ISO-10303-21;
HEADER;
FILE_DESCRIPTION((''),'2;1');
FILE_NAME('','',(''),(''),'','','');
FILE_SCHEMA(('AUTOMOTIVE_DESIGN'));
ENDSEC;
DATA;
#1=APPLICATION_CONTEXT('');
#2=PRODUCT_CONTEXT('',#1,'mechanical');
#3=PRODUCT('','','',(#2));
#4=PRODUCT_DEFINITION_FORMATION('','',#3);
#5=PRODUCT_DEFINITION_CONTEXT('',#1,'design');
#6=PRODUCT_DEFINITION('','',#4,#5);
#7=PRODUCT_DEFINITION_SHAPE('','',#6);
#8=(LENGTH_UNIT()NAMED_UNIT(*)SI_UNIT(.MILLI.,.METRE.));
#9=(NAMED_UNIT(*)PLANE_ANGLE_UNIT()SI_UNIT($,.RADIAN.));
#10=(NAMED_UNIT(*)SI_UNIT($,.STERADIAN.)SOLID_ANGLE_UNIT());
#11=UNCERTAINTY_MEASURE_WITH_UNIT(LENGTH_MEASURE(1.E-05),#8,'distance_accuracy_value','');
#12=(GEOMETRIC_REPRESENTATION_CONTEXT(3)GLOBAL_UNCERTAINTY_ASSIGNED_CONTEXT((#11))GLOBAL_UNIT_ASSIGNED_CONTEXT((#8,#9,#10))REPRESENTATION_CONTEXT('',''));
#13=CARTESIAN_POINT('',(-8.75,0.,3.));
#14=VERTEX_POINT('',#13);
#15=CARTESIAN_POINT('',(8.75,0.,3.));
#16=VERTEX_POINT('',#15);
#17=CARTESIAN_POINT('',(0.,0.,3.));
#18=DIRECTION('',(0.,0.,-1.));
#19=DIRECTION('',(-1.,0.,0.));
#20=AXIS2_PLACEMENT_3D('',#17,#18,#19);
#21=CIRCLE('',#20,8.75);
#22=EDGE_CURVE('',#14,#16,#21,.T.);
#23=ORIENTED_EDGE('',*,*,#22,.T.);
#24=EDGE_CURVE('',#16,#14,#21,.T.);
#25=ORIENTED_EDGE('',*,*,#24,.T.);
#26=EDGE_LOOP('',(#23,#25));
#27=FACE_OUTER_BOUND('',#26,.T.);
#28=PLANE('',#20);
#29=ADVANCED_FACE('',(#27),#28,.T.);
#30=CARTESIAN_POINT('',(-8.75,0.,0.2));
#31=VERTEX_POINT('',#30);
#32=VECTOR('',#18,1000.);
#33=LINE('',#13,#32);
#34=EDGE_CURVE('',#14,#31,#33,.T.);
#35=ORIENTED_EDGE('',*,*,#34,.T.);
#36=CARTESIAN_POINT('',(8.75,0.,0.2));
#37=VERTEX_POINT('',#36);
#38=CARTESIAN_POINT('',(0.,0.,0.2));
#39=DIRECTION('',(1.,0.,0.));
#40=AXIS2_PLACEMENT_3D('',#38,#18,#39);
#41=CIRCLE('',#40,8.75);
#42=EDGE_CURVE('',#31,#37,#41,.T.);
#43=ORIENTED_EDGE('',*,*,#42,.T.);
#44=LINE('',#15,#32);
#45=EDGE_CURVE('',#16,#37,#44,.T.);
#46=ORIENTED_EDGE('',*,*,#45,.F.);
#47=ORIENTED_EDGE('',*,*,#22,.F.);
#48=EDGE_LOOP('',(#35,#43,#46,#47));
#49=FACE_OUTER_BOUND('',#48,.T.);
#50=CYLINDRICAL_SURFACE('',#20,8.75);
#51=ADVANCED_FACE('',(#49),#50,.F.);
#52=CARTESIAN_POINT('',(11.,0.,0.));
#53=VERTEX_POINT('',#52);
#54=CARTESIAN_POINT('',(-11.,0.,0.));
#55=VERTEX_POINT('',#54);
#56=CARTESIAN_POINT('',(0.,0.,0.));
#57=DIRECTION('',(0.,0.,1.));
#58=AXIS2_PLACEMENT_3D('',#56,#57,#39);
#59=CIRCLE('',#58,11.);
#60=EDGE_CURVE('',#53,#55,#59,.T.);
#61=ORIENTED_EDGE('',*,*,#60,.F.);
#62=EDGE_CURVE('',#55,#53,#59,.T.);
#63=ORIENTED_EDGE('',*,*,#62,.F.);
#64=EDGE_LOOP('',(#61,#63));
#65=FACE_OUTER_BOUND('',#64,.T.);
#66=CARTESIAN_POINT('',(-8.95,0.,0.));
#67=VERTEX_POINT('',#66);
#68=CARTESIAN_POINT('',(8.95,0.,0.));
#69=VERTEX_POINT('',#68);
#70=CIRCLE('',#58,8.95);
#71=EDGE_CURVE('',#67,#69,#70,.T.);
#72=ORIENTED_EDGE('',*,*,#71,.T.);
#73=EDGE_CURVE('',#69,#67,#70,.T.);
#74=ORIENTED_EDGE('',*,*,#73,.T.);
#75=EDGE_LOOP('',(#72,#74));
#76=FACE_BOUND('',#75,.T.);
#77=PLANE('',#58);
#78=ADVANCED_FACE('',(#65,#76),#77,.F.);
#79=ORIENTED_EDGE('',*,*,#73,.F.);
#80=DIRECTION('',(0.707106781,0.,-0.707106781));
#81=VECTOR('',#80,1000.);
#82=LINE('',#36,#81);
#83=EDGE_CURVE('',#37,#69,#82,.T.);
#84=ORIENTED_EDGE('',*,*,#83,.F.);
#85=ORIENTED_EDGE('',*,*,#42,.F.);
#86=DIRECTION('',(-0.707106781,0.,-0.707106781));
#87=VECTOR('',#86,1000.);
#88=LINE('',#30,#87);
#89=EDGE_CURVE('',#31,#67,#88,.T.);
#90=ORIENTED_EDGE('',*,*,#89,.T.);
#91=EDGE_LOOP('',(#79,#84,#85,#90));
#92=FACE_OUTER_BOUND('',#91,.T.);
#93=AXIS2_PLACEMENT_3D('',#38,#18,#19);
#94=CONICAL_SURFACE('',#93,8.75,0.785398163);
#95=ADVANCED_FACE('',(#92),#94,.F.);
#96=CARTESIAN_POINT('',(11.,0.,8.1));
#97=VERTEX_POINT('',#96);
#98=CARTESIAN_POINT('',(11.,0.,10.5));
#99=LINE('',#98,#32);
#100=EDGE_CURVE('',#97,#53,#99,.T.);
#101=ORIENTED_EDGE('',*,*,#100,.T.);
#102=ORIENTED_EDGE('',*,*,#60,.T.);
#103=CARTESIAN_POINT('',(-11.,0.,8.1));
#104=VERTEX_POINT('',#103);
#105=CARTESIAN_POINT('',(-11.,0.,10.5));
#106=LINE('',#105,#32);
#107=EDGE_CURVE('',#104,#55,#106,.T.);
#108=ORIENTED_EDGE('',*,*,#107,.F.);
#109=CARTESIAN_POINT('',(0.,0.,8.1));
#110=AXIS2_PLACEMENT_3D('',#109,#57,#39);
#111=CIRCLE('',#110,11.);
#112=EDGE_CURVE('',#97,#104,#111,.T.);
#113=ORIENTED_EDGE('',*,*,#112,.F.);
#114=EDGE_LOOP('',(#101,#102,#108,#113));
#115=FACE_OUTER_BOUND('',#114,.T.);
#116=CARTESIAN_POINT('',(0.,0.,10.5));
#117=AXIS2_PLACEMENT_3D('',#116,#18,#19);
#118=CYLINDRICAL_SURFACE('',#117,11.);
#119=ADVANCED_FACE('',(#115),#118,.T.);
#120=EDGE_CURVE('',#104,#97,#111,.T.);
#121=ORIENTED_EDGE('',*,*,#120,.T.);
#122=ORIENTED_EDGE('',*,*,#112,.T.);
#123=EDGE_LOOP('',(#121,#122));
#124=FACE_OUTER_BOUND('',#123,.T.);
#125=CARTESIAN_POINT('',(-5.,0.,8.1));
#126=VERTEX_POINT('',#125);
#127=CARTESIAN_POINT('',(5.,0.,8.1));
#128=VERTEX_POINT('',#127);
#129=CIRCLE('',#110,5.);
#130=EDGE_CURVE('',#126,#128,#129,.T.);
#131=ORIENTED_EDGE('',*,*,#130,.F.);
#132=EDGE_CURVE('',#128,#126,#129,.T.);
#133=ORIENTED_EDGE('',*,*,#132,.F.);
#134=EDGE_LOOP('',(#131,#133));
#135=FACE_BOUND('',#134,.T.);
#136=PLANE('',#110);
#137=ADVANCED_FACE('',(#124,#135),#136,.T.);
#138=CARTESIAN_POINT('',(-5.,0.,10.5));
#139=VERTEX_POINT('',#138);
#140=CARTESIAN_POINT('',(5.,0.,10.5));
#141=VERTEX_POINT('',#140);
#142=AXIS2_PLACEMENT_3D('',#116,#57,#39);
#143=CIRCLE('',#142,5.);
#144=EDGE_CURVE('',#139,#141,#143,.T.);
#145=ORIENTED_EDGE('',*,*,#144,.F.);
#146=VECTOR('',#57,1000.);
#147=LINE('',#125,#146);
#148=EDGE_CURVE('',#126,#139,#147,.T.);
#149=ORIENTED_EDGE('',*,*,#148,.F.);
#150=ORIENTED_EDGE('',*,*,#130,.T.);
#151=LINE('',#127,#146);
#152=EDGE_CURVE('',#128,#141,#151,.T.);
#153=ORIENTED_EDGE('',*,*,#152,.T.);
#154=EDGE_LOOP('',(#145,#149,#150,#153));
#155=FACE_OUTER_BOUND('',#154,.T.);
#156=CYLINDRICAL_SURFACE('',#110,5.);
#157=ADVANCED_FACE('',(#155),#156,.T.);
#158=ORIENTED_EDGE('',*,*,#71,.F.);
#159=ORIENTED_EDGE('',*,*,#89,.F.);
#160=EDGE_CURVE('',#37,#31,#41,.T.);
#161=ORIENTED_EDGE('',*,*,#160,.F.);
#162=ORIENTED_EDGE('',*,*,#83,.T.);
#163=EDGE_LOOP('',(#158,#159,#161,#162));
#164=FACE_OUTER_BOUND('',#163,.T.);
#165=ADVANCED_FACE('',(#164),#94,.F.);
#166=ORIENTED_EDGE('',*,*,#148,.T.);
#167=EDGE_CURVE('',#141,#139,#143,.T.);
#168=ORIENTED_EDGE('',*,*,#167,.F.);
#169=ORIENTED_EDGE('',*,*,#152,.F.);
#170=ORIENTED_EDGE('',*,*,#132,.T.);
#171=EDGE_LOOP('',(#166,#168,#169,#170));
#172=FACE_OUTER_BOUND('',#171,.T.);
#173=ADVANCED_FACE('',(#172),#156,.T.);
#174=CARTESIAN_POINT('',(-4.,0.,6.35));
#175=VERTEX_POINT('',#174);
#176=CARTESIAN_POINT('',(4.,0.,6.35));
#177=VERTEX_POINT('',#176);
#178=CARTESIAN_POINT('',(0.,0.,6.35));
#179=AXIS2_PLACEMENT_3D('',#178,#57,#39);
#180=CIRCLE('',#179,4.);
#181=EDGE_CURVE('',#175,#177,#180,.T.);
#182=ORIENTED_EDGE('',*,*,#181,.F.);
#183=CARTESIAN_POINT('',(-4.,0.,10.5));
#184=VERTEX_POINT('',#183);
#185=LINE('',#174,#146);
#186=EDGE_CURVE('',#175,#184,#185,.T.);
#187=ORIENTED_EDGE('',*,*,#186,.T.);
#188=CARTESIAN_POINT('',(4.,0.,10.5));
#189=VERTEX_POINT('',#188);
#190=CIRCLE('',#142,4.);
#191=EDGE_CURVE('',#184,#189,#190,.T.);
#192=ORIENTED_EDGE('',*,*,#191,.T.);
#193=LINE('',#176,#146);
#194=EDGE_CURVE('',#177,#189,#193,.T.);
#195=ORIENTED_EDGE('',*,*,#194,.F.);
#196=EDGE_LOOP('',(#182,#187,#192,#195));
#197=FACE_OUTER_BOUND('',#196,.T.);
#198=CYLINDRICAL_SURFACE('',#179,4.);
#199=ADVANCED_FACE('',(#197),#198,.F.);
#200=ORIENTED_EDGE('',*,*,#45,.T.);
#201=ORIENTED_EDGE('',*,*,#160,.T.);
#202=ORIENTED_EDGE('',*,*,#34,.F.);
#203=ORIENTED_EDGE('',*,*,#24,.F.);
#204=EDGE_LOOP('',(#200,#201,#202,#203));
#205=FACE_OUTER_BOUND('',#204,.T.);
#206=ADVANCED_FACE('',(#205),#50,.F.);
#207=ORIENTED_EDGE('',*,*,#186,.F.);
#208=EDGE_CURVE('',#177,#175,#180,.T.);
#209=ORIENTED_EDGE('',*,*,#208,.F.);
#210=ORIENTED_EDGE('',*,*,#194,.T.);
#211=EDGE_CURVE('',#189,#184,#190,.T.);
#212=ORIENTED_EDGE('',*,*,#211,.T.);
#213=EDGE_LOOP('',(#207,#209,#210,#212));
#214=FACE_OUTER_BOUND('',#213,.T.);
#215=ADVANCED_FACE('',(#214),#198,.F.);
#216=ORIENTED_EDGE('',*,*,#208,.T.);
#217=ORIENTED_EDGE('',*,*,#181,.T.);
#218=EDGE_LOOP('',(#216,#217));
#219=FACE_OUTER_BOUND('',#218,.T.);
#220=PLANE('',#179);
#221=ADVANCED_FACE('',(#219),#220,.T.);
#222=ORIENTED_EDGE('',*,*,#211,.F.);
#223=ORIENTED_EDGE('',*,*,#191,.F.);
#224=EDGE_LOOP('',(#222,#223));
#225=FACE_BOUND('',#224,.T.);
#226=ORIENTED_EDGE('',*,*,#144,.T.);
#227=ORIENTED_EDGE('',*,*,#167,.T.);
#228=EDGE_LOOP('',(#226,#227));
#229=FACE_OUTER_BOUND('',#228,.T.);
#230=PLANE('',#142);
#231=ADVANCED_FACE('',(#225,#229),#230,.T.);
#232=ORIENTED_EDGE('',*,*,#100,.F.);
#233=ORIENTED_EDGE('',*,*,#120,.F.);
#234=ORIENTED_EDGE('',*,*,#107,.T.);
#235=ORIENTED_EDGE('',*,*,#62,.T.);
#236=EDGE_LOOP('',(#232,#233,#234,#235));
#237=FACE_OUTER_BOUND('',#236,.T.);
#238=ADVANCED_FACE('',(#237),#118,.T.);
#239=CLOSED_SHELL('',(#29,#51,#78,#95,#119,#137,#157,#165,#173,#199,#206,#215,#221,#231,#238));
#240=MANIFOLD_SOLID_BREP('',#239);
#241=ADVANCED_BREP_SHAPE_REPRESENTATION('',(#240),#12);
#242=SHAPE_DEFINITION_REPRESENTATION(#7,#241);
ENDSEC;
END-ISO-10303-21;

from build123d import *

# Parameters (mm, degrees)
SKETCH1_R           = 11
BOSS_EXTRUDE1_DEPTH = 10.5
SKETCH2_OUTSIDE_W   = 30.568
SKETCH2_OUTSIDE_H   = 30.568
SKETCH2_OUTSIDE_R   = 5
CUT_EXTRUDE1_DEPTH  = 2.4
SKETCH3_R           = 4
CUT_EXTRUDE2_DEPTH  = 4.15
SKETCH4_R           = 8.75
CUT_EXTRUDE3_DEPTH  = 3
CHAMFER1_SIZE       = 0.2


with BuildPart() as part:
    # Sketch1 → Boss-Extrude1 (new body)
    with BuildSketch(Plane.XY):
        with Locations(Location((0, 0, 0), (0, 0, 180))):
            Circle(SKETCH1_R)
    extrude(amount=BOSS_EXTRUDE1_DEPTH)

    # Sketch2 outside → Cut-Extrude1 (cut)
    with BuildSketch(Plane.XY.offset(10.5)):
        Rectangle(SKETCH2_OUTSIDE_W, SKETCH2_OUTSIDE_H)
        Circle(SKETCH2_OUTSIDE_R, mode=Mode.SUBTRACT)
    extrude(amount=-CUT_EXTRUDE1_DEPTH, mode=Mode.SUBTRACT)

    # Sketch3 → Cut-Extrude2 (cut)
    with BuildSketch(Plane.XY.offset(10.5)):
        Circle(SKETCH3_R)
    extrude(amount=-CUT_EXTRUDE2_DEPTH, mode=Mode.SUBTRACT)

    # Sketch4 → Cut-Extrude3 (cut)
    with BuildSketch(Plane(origin=(0, 0, 0), x_dir=(-1, 0, 0), z_dir=(0, 0, -1))):
        Circle(SKETCH4_R)
    extrude(amount=-CUT_EXTRUDE3_DEPTH, mode=Mode.SUBTRACT)

    # Chamfer1
    chamfer1_edges = [part.edges().sort_by_distance(p)[0] for p in [
        (8.75, 0, 0),
    ]]
    chamfer(chamfer1_edges, length=CHAMFER1_SIZE)


solid = part.part
